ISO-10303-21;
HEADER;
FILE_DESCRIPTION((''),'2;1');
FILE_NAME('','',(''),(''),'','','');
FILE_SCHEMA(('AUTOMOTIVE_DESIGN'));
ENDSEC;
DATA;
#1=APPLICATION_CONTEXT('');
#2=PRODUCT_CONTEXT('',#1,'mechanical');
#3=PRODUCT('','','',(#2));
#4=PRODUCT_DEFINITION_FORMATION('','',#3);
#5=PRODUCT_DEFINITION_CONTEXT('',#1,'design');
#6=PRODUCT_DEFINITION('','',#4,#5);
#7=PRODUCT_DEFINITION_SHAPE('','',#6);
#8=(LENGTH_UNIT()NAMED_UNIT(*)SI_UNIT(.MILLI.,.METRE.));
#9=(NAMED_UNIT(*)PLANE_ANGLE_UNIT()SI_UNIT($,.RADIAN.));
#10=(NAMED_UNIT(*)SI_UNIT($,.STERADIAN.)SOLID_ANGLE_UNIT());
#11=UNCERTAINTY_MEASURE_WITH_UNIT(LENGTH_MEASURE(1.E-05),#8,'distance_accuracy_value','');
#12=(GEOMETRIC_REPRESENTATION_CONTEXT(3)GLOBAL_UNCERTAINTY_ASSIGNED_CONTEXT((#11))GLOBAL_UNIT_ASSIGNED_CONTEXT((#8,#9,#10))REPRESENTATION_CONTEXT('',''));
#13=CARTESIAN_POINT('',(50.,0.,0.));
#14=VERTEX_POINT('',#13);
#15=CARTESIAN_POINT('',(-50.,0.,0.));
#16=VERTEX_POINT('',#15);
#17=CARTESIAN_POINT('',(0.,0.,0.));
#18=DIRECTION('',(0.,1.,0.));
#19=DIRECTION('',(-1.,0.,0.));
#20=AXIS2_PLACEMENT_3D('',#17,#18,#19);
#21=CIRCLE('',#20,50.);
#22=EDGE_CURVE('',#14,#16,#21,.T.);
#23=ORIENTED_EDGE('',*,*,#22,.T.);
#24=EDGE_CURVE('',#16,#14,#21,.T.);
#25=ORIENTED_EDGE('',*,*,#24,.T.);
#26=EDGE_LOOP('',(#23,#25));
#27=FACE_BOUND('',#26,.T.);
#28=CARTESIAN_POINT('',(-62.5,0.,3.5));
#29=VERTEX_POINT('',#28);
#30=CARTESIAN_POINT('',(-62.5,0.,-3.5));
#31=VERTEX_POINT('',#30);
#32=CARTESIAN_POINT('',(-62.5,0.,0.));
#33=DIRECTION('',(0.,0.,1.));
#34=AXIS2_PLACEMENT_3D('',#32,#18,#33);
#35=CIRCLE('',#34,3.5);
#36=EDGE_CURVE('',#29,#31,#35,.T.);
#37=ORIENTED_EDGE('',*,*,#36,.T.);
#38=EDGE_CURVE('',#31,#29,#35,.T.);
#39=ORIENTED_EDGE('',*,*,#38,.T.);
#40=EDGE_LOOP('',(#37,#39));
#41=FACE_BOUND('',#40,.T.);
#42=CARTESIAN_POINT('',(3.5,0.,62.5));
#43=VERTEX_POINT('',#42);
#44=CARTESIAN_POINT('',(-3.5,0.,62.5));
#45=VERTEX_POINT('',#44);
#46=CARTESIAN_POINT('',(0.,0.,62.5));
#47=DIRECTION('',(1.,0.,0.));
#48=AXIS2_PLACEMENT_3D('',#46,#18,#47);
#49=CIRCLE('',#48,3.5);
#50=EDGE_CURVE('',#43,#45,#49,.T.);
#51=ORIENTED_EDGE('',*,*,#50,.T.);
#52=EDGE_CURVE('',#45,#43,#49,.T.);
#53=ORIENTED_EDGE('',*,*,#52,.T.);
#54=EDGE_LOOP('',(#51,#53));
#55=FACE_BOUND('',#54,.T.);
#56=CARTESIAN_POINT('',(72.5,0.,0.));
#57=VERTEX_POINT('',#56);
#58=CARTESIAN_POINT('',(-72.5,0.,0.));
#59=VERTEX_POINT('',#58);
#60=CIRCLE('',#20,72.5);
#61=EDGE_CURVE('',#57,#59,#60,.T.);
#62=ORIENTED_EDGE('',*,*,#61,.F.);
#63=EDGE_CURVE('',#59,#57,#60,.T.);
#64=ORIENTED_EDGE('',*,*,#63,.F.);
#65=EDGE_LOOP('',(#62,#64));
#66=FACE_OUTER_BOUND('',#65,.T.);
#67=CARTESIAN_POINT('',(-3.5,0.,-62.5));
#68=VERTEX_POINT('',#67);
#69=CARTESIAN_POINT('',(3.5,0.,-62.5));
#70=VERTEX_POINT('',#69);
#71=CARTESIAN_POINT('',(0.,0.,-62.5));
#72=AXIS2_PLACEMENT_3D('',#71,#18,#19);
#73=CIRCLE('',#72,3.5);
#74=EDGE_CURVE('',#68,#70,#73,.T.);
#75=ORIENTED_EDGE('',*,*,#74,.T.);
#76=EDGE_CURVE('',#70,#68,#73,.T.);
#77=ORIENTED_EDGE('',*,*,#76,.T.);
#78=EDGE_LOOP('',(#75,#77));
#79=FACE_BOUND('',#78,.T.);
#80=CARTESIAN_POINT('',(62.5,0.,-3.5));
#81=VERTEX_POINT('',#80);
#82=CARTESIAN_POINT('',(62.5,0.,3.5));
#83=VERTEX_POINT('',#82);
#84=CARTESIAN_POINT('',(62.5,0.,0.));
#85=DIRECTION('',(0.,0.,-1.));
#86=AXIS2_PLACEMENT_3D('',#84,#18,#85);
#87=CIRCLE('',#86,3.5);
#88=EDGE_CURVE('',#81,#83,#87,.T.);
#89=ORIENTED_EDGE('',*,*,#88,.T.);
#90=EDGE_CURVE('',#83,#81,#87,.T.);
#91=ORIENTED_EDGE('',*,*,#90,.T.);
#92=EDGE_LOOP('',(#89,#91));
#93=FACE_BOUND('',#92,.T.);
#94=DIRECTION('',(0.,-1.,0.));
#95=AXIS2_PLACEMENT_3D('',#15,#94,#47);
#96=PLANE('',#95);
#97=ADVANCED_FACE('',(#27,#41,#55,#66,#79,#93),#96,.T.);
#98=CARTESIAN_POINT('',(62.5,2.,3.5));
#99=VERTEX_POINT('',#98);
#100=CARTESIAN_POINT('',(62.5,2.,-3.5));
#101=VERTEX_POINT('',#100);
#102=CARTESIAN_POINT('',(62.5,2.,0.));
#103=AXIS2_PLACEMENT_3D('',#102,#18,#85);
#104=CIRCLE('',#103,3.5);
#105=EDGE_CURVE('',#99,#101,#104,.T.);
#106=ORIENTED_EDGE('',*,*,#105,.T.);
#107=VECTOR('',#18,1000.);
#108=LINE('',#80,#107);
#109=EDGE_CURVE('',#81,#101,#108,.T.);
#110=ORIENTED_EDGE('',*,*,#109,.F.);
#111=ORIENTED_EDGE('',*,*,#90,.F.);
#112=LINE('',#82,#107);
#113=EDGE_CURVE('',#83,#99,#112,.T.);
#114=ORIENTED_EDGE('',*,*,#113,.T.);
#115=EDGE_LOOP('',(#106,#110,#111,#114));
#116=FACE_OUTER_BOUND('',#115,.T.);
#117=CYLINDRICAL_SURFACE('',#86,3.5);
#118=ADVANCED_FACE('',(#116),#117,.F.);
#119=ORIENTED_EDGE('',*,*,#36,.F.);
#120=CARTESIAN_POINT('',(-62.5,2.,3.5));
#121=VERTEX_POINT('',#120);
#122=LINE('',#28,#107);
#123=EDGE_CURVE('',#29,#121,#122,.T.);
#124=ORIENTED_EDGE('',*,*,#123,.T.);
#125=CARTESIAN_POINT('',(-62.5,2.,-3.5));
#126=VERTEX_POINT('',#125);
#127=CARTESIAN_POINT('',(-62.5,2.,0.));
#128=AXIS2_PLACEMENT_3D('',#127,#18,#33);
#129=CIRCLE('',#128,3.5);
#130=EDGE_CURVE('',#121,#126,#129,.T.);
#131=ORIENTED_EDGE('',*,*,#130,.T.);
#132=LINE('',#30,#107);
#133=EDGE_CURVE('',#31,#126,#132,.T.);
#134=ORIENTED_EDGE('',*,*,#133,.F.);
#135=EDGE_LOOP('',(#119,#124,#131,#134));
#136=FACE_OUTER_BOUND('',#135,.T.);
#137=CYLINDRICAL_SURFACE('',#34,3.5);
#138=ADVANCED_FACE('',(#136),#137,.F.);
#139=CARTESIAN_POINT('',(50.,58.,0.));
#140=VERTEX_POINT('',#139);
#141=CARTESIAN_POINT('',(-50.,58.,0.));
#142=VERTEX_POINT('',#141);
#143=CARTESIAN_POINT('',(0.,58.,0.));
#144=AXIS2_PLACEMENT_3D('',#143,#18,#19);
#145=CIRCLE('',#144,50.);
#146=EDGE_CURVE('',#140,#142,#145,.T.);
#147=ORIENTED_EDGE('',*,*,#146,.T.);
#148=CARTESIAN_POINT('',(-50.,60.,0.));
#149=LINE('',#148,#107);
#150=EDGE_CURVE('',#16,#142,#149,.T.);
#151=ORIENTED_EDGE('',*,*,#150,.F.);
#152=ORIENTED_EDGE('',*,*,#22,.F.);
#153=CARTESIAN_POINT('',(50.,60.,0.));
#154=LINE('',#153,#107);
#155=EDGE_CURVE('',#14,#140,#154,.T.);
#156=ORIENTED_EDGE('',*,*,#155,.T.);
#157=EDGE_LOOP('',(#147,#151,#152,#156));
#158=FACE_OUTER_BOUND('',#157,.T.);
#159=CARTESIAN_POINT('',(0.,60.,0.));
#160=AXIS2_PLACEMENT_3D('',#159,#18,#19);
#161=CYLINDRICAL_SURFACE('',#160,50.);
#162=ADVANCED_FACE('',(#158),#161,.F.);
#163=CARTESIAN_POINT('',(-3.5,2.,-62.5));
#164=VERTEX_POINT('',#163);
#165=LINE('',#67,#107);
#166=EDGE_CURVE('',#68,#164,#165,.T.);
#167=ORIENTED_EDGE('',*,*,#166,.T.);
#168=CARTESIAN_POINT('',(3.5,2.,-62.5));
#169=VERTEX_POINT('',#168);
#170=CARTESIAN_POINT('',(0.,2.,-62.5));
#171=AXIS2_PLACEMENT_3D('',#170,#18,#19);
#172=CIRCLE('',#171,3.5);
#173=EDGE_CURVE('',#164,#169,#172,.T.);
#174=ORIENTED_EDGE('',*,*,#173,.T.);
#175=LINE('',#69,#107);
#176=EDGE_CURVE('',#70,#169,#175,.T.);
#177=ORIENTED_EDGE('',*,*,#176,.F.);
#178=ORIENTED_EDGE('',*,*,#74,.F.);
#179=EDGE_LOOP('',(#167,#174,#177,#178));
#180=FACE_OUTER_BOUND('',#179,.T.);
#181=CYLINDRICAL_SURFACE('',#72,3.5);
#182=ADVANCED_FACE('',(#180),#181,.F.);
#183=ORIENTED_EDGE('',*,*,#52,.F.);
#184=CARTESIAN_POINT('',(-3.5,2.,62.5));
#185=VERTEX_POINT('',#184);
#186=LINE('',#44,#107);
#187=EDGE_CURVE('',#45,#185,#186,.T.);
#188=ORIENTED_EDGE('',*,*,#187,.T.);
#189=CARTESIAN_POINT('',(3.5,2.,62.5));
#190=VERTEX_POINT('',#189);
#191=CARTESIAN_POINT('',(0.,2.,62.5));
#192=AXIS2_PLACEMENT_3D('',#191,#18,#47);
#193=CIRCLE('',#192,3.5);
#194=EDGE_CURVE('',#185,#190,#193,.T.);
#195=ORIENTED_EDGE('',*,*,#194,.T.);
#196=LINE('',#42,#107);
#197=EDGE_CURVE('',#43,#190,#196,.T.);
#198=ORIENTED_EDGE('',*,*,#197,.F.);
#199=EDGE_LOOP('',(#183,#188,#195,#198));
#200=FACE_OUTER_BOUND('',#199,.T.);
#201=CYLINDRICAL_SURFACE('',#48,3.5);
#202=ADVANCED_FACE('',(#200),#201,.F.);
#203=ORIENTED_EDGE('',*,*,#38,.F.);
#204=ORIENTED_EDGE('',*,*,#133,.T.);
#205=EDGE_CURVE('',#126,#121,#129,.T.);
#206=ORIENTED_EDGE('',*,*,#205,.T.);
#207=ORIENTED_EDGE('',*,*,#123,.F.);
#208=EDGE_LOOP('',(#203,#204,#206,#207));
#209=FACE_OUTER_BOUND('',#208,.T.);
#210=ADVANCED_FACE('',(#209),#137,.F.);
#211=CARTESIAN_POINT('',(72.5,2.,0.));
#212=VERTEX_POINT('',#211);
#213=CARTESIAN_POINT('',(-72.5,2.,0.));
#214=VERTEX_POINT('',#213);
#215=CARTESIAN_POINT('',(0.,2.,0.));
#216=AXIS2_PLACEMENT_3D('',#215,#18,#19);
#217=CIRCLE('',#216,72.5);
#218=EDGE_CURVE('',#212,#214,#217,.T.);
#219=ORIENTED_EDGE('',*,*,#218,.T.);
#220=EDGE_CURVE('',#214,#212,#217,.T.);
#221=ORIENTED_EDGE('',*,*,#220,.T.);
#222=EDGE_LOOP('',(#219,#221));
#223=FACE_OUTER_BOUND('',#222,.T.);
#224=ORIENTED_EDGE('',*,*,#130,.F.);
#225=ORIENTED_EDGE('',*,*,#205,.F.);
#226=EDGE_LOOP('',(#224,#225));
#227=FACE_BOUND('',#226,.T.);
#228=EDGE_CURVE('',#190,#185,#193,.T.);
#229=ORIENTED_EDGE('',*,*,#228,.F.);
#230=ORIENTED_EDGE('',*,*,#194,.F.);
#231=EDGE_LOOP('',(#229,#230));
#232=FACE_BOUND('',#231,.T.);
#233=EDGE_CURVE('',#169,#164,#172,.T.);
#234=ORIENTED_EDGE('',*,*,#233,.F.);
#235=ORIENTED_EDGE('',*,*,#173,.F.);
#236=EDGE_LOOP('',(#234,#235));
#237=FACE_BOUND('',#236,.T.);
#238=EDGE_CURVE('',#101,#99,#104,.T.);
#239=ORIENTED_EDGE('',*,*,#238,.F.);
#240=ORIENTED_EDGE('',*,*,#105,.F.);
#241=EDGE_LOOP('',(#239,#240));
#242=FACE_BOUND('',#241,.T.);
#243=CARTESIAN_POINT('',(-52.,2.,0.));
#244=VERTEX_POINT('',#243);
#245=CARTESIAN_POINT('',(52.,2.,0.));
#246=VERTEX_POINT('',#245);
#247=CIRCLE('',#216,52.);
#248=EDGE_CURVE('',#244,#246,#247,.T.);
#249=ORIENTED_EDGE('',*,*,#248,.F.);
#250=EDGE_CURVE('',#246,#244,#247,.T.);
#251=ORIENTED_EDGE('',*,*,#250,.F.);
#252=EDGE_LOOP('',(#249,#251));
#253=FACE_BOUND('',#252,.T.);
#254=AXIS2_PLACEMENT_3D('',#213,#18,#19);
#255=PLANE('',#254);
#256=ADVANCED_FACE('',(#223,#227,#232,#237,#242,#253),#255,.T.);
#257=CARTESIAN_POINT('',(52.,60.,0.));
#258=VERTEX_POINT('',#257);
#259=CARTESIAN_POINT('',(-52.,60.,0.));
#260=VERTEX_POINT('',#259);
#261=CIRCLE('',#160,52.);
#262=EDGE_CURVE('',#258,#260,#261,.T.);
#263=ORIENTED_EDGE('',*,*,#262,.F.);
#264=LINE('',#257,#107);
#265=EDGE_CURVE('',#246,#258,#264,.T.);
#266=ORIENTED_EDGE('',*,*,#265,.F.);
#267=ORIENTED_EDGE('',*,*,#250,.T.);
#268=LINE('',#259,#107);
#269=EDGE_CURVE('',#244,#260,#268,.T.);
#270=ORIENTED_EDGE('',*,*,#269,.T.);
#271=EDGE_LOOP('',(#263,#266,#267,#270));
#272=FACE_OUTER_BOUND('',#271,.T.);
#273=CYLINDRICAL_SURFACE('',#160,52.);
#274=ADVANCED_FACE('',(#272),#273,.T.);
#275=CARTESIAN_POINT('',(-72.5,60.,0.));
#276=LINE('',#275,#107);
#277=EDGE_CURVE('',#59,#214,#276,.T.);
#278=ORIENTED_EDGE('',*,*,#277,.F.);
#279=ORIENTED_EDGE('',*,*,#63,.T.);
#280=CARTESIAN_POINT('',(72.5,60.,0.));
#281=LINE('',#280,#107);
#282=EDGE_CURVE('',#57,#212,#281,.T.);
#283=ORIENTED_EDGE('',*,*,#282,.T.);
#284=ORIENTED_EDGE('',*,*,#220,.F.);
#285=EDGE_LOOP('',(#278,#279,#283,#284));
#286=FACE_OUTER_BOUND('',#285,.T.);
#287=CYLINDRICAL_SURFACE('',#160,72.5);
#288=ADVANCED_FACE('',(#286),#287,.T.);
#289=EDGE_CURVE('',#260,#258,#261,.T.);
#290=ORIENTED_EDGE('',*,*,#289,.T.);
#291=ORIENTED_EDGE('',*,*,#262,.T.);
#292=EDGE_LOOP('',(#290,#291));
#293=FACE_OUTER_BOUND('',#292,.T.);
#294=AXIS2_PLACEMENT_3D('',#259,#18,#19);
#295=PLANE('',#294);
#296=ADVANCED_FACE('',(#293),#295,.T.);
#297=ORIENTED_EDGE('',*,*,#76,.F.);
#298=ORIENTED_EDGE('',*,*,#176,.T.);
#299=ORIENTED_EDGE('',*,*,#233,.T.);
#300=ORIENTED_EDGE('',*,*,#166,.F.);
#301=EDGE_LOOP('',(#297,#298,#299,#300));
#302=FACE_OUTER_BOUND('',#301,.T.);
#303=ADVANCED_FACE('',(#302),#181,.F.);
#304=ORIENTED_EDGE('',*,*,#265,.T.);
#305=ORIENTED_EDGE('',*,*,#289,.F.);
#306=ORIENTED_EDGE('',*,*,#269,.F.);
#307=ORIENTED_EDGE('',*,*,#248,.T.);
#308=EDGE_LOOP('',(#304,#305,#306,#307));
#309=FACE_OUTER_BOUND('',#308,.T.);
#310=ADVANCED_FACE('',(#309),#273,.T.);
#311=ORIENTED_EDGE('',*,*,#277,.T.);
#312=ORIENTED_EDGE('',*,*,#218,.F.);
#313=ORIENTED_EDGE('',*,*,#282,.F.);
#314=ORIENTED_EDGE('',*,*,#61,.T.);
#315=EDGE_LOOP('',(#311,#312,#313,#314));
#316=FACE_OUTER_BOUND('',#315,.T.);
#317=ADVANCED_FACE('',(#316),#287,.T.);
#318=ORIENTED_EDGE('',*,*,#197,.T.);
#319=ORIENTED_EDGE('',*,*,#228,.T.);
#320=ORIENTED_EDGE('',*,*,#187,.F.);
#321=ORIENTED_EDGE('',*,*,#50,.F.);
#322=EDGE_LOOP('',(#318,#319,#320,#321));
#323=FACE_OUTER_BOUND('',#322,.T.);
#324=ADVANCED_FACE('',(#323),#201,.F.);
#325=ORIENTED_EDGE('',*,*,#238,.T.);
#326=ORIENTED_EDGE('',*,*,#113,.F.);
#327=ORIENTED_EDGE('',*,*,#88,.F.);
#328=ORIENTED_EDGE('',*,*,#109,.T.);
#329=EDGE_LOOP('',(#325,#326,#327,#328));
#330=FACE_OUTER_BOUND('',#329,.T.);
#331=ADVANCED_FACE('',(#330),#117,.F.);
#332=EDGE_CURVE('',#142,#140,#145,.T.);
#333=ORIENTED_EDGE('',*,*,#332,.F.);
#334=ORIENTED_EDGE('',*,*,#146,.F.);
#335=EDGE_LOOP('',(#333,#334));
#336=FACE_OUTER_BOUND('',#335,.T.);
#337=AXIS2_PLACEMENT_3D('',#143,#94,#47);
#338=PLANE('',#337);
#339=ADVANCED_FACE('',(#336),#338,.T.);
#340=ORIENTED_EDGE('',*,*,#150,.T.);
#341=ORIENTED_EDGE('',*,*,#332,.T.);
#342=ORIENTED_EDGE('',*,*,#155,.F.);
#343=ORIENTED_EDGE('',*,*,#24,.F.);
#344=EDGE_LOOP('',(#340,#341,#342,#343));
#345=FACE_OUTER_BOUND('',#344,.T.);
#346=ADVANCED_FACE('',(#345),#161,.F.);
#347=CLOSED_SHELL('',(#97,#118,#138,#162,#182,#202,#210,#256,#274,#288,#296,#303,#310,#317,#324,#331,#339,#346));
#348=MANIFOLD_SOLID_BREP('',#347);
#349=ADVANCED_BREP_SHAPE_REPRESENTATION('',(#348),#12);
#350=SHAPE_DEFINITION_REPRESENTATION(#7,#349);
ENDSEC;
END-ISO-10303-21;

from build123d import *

# Parameters (mm, degrees)
SKETCH2_R          = 3.5
CUT_EXTRUDE1_DEPTH = 118.798556867
CIRPATTERN1_COUNT  = 4


with BuildPart() as part:
    # Sketch1 → Revolve1 (revolve)
    with BuildSketch(Plane.XY):
        Polygon((-50, 0), (-72.5, 0), (-72.5, 2), (-52, 2), (-52, 60), (0, 60), (0, 58), (-50, 58), align=None)
    revolve(axis=Axis((0, 60, 0), (0, -1, 0)))

    # Sketch2 → Cut-Extrude1 (cut, through all)
    with BuildSketch(Plane(origin=(0, 2, 0), x_dir=(1, 0, 0), z_dir=(0, 1, 0))):
        with Locations(Location((0, 62.5, 0), (0, 0, 180))):
            Circle(SKETCH2_R)
    cut_extrude1 = extrude(amount=-CUT_EXTRUDE1_DEPTH, mode=Mode.SUBTRACT)

    # CirPattern1: Cut-Extrude1 ×4 about axis
    cirpattern1_axis = Axis((0, 0, 0), (0, 1, 0))
    for i in range(1, CIRPATTERN1_COUNT):
        add(cut_extrude1.rotate(cirpattern1_axis, i * 360 / CIRPATTERN1_COUNT), mode=Mode.SUBTRACT)


solid = part.part
